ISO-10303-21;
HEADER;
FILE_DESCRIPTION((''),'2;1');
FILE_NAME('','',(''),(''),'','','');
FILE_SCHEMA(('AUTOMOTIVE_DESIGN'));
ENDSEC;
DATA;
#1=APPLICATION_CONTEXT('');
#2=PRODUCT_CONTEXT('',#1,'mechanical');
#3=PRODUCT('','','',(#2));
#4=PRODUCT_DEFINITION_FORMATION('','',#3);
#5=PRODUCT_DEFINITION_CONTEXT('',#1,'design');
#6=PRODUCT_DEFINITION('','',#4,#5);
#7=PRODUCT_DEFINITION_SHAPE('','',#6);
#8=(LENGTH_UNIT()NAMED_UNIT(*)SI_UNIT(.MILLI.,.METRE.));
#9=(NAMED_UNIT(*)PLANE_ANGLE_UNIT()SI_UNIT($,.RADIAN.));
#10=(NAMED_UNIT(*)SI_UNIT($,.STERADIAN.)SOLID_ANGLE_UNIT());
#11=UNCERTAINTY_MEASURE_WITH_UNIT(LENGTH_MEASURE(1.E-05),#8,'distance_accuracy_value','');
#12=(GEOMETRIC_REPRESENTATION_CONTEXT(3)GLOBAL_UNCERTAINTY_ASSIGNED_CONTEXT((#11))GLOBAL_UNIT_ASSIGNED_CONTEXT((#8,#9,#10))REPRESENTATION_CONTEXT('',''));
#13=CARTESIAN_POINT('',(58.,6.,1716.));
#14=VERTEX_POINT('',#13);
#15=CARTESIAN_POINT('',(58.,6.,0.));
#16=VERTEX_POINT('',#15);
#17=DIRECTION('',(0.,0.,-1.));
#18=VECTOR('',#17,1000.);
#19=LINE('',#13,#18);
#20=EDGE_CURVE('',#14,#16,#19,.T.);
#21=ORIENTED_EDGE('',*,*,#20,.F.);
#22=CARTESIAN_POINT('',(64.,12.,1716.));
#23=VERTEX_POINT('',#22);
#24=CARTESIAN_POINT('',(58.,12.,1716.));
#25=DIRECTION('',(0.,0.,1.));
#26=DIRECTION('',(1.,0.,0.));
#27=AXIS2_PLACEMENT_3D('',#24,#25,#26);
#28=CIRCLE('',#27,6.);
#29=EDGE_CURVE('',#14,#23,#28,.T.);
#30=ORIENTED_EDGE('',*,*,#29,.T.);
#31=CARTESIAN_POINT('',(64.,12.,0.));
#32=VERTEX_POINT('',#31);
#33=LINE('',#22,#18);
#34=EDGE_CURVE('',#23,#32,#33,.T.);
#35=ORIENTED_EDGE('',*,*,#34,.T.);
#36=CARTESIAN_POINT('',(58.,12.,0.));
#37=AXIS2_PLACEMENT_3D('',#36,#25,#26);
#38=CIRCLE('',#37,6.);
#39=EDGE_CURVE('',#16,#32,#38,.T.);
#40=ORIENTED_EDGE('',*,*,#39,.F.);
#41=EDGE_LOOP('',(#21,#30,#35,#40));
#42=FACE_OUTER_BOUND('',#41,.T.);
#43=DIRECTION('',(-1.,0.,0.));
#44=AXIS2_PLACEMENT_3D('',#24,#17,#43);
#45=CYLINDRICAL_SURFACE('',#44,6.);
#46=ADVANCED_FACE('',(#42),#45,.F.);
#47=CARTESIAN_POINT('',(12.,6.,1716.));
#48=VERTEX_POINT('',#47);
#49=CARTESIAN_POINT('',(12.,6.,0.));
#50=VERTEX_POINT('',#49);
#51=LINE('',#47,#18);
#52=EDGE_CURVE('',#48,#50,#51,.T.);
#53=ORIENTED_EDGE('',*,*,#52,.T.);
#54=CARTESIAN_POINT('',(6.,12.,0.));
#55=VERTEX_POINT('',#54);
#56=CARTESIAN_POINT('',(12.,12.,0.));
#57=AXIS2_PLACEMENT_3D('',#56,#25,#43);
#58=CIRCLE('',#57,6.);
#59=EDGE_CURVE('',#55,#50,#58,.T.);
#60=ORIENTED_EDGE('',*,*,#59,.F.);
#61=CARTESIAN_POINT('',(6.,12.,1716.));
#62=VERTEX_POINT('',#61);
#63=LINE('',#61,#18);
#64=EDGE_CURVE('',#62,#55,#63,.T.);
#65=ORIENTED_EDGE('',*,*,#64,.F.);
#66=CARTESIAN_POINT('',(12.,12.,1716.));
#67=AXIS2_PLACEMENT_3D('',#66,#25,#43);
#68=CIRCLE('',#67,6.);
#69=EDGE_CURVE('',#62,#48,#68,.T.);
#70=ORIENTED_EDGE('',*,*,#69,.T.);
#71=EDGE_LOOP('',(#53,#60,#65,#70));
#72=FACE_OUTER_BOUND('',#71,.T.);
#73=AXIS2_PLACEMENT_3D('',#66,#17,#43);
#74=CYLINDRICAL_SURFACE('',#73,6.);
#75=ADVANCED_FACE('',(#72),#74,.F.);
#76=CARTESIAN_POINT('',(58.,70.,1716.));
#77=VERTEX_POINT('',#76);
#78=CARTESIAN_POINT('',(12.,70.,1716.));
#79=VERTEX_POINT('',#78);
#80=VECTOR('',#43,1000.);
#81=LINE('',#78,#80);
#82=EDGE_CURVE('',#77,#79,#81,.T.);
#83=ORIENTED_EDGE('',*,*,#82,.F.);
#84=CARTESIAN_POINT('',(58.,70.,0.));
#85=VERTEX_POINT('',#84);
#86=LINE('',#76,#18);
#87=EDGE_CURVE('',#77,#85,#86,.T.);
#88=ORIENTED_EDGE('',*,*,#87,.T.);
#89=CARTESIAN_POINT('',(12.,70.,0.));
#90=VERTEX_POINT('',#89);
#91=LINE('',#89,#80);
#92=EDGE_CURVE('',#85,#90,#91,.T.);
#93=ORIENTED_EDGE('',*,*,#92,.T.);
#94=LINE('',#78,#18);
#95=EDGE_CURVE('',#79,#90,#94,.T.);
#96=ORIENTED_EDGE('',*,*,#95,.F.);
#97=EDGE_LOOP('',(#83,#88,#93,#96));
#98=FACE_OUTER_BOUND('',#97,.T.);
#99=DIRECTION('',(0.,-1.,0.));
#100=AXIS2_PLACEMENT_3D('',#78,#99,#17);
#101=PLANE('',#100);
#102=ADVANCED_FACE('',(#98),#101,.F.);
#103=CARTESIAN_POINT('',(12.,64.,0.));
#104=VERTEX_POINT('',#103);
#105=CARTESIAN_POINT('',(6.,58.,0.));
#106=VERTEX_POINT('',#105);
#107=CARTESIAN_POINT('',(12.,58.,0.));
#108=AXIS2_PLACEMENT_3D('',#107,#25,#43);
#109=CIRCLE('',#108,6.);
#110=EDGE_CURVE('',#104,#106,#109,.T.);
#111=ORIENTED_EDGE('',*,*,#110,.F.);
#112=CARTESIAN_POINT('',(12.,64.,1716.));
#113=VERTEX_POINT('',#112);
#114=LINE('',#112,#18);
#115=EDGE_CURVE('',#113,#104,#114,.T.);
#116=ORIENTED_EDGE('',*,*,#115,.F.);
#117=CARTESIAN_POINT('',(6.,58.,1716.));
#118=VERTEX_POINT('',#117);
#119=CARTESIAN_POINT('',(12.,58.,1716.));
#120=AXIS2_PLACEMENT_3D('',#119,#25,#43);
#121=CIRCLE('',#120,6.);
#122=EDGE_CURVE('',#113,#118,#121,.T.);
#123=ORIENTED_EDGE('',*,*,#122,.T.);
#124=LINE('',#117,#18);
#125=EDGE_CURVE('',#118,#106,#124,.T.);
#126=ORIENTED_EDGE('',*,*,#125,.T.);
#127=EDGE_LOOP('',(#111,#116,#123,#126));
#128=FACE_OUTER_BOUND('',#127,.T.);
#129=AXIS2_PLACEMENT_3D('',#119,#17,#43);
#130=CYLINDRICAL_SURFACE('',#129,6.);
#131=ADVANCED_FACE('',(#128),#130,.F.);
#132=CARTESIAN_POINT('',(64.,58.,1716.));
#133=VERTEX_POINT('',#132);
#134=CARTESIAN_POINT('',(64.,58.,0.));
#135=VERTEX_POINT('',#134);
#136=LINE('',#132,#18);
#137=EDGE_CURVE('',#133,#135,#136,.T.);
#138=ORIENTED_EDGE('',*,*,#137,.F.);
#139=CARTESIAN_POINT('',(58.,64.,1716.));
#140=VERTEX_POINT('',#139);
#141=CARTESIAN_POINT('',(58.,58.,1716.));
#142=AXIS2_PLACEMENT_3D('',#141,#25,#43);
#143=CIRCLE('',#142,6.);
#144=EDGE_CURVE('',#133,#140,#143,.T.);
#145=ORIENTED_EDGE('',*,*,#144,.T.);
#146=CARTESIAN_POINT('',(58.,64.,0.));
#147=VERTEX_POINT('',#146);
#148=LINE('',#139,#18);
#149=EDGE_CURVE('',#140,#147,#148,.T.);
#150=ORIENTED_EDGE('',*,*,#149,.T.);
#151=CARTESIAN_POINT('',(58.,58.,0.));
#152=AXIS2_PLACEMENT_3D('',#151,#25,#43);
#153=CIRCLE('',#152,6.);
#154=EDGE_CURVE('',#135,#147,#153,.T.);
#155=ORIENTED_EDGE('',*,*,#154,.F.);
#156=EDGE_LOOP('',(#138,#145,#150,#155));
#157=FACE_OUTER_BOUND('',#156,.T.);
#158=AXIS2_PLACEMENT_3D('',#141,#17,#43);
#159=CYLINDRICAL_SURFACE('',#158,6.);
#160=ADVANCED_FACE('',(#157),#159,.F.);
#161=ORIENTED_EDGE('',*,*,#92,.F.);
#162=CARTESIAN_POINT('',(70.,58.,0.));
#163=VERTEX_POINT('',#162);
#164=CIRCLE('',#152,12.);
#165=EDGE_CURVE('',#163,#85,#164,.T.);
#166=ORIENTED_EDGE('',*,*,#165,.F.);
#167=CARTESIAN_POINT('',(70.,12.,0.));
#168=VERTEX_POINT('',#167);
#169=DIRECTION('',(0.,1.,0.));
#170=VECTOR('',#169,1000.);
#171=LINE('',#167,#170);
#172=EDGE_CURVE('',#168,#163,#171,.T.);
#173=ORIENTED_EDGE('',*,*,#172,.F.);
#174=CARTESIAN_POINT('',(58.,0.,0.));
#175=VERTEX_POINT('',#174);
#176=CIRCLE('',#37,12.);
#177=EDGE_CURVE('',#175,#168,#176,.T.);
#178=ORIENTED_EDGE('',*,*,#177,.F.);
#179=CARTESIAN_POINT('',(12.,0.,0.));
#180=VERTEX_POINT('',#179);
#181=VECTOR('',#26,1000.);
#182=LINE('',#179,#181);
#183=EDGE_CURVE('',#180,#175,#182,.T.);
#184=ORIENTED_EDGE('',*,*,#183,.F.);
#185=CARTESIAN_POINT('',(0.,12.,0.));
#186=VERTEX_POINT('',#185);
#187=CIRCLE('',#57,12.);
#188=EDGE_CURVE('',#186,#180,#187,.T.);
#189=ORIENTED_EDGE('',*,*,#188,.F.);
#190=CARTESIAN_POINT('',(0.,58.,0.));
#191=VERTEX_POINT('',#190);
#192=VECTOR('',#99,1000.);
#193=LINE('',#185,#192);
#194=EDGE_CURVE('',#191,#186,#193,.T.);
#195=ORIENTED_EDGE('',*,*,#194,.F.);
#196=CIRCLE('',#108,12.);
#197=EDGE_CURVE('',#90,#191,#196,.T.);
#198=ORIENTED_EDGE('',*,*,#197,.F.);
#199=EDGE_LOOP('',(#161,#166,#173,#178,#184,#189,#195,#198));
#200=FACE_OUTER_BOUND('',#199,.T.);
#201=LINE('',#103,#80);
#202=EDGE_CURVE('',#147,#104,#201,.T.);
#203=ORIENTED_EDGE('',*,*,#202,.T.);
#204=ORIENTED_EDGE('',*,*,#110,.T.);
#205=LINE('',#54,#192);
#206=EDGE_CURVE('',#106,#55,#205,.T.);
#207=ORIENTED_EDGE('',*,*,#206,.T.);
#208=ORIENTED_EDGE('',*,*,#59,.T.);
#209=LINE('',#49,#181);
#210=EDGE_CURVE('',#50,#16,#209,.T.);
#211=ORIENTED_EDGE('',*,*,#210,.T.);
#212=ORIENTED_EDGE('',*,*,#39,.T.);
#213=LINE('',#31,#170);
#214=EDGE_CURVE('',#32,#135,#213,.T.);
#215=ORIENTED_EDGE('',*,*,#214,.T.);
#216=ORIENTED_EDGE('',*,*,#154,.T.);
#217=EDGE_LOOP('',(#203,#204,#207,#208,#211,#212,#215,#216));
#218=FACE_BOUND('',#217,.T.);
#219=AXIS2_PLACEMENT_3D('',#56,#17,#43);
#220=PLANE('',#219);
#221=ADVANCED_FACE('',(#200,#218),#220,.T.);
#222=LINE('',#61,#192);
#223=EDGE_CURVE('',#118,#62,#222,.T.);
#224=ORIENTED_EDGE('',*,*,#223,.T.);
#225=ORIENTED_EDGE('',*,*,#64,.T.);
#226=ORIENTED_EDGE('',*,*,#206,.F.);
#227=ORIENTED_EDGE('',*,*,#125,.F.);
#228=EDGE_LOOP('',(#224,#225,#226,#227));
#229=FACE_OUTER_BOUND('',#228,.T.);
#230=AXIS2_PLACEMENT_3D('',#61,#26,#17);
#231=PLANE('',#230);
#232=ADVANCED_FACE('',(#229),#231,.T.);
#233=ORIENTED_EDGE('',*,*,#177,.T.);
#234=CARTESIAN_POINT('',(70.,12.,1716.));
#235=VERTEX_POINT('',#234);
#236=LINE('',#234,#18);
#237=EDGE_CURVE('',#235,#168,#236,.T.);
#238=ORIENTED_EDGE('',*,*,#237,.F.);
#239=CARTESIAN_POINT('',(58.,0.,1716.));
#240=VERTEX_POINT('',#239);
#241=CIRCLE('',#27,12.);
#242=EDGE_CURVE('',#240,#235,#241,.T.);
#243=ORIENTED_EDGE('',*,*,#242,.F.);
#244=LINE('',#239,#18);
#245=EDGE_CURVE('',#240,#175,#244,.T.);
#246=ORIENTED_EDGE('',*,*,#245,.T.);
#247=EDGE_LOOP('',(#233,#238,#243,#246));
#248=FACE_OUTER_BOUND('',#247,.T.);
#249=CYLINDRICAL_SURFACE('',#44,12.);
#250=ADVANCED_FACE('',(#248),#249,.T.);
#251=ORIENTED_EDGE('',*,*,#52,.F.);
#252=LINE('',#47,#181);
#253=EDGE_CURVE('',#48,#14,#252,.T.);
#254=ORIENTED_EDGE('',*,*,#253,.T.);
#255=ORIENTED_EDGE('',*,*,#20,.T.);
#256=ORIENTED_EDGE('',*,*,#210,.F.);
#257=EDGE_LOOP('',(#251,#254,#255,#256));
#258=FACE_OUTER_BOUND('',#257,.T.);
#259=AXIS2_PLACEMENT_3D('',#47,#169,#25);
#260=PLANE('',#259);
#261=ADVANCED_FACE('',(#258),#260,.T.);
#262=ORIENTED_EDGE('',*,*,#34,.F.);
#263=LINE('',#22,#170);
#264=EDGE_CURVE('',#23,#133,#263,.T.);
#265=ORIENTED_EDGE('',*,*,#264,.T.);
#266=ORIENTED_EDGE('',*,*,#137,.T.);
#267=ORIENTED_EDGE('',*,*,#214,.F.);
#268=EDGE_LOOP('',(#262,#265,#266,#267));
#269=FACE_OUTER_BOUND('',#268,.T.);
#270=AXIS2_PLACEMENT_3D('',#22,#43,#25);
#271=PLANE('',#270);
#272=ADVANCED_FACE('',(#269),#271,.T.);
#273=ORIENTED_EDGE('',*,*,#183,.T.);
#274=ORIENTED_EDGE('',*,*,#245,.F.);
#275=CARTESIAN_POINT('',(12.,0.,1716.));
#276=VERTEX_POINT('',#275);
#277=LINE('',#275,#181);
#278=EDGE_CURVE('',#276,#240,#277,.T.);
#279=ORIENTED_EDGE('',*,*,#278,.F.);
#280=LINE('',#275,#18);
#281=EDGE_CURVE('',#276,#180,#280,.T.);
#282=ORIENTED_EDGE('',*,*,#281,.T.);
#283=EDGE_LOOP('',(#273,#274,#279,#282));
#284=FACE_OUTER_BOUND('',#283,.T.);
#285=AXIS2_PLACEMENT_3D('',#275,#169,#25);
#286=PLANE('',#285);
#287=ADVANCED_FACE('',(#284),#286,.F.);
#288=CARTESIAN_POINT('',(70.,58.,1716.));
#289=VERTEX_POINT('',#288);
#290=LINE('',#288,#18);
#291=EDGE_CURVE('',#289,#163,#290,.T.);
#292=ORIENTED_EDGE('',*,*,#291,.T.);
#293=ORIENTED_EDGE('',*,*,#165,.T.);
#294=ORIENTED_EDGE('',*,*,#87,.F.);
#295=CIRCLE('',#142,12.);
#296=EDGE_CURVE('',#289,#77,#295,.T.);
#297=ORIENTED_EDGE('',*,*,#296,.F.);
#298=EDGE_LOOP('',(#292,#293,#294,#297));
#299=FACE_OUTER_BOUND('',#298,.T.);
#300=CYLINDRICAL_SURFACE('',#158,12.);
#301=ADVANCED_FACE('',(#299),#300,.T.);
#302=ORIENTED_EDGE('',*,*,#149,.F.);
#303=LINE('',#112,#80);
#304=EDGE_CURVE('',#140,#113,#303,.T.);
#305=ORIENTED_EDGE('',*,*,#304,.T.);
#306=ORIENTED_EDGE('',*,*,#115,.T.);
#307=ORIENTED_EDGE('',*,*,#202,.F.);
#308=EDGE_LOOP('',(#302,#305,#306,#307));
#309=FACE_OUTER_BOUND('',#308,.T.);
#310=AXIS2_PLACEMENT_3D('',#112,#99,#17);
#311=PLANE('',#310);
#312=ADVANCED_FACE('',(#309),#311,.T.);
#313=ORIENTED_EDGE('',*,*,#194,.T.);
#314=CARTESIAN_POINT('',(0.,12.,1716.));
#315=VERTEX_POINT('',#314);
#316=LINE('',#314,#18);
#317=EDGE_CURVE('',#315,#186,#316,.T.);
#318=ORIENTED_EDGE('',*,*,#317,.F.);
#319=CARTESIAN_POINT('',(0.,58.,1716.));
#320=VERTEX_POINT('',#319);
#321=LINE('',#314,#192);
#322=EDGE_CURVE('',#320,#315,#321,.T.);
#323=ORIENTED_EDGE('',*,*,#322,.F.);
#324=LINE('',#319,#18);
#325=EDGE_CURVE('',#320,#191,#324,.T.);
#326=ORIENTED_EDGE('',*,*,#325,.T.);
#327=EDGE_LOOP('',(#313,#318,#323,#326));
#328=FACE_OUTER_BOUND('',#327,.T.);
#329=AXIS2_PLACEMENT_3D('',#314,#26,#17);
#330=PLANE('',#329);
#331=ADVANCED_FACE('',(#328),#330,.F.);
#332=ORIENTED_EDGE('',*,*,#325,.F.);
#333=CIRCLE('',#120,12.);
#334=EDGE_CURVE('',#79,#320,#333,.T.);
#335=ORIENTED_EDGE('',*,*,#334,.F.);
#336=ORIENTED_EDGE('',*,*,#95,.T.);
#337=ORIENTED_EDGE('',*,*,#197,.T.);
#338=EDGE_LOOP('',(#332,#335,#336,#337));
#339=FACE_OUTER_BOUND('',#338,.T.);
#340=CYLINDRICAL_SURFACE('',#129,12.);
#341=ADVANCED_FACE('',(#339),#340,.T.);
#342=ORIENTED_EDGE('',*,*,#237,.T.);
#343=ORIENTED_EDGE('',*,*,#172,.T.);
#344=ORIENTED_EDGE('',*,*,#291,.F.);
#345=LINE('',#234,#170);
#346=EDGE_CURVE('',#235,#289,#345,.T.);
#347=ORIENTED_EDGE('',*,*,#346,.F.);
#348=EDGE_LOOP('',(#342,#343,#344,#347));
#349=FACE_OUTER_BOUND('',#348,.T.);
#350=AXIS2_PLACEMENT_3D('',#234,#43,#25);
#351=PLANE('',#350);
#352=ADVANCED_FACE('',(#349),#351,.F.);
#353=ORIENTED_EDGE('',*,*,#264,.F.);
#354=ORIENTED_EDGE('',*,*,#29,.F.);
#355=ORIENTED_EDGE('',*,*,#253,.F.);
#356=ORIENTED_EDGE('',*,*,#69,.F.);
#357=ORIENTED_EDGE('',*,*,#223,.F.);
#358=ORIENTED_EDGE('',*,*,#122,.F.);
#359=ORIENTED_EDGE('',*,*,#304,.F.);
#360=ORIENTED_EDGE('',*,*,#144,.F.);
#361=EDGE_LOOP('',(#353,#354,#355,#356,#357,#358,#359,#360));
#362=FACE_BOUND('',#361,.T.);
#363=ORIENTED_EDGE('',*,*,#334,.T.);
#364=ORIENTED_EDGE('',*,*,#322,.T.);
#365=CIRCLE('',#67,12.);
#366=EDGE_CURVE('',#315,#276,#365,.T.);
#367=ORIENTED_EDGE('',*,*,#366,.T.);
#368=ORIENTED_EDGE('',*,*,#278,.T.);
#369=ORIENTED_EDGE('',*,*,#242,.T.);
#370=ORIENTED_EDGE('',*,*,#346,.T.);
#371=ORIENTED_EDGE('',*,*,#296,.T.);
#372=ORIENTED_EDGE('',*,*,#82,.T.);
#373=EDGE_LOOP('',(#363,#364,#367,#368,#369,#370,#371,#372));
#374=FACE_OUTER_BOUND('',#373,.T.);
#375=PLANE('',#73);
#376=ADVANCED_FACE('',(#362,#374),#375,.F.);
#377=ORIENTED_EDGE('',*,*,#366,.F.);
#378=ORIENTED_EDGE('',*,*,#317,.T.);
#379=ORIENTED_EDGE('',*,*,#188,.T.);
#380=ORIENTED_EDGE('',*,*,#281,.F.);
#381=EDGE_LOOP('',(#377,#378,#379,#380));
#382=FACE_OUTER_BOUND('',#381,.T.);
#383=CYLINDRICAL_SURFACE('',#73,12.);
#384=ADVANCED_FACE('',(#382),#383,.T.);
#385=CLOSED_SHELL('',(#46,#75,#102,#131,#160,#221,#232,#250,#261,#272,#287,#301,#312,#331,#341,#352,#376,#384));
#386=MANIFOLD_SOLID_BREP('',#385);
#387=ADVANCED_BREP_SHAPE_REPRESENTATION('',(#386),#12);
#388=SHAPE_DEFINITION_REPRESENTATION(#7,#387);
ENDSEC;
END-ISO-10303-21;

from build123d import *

# Parameters (mm, degrees)
BOSS_EXTRUDE1_DEPTH = 1716


with BuildPart() as part:
    # Sketch1 → Boss-Extrude1 (new body)
    with BuildSketch(Plane.XY):
        with BuildLine():
            Line((12, 0), (58, 0))
            ThreePointArc((58, 0), (66.485281374, 3.514718626), (70, 12))
            Line((70, 12), (70, 58))
            ThreePointArc((70, 58), (66.485281374, 66.485281374), (58, 70))
            Line((58, 70), (12, 70))
            ThreePointArc((12, 70), (3.514718626, 66.485281374), (0, 58))
            Line((0, 58), (0, 12))
            ThreePointArc((0, 12), (3.514718626, 3.514718626), (12, 0))
        make_face()
        with BuildLine():
            Line((12, 6), (58, 6))
            ThreePointArc((58, 6), (62.242640687, 7.757359313), (64, 12))
            Line((64, 12), (64, 58))
            ThreePointArc((64, 58), (62.242640687, 62.242640687), (58, 64))
            Line((58, 64), (12, 64))
            ThreePointArc((12, 64), (7.757359313, 62.242640687), (6, 58))
            Line((6, 58), (6, 12))
            ThreePointArc((6, 12), (7.757359313, 7.757359313), (12, 6))
        make_face(mode=Mode.SUBTRACT)
    extrude(amount=BOSS_EXTRUDE1_DEPTH)


solid = part.part
